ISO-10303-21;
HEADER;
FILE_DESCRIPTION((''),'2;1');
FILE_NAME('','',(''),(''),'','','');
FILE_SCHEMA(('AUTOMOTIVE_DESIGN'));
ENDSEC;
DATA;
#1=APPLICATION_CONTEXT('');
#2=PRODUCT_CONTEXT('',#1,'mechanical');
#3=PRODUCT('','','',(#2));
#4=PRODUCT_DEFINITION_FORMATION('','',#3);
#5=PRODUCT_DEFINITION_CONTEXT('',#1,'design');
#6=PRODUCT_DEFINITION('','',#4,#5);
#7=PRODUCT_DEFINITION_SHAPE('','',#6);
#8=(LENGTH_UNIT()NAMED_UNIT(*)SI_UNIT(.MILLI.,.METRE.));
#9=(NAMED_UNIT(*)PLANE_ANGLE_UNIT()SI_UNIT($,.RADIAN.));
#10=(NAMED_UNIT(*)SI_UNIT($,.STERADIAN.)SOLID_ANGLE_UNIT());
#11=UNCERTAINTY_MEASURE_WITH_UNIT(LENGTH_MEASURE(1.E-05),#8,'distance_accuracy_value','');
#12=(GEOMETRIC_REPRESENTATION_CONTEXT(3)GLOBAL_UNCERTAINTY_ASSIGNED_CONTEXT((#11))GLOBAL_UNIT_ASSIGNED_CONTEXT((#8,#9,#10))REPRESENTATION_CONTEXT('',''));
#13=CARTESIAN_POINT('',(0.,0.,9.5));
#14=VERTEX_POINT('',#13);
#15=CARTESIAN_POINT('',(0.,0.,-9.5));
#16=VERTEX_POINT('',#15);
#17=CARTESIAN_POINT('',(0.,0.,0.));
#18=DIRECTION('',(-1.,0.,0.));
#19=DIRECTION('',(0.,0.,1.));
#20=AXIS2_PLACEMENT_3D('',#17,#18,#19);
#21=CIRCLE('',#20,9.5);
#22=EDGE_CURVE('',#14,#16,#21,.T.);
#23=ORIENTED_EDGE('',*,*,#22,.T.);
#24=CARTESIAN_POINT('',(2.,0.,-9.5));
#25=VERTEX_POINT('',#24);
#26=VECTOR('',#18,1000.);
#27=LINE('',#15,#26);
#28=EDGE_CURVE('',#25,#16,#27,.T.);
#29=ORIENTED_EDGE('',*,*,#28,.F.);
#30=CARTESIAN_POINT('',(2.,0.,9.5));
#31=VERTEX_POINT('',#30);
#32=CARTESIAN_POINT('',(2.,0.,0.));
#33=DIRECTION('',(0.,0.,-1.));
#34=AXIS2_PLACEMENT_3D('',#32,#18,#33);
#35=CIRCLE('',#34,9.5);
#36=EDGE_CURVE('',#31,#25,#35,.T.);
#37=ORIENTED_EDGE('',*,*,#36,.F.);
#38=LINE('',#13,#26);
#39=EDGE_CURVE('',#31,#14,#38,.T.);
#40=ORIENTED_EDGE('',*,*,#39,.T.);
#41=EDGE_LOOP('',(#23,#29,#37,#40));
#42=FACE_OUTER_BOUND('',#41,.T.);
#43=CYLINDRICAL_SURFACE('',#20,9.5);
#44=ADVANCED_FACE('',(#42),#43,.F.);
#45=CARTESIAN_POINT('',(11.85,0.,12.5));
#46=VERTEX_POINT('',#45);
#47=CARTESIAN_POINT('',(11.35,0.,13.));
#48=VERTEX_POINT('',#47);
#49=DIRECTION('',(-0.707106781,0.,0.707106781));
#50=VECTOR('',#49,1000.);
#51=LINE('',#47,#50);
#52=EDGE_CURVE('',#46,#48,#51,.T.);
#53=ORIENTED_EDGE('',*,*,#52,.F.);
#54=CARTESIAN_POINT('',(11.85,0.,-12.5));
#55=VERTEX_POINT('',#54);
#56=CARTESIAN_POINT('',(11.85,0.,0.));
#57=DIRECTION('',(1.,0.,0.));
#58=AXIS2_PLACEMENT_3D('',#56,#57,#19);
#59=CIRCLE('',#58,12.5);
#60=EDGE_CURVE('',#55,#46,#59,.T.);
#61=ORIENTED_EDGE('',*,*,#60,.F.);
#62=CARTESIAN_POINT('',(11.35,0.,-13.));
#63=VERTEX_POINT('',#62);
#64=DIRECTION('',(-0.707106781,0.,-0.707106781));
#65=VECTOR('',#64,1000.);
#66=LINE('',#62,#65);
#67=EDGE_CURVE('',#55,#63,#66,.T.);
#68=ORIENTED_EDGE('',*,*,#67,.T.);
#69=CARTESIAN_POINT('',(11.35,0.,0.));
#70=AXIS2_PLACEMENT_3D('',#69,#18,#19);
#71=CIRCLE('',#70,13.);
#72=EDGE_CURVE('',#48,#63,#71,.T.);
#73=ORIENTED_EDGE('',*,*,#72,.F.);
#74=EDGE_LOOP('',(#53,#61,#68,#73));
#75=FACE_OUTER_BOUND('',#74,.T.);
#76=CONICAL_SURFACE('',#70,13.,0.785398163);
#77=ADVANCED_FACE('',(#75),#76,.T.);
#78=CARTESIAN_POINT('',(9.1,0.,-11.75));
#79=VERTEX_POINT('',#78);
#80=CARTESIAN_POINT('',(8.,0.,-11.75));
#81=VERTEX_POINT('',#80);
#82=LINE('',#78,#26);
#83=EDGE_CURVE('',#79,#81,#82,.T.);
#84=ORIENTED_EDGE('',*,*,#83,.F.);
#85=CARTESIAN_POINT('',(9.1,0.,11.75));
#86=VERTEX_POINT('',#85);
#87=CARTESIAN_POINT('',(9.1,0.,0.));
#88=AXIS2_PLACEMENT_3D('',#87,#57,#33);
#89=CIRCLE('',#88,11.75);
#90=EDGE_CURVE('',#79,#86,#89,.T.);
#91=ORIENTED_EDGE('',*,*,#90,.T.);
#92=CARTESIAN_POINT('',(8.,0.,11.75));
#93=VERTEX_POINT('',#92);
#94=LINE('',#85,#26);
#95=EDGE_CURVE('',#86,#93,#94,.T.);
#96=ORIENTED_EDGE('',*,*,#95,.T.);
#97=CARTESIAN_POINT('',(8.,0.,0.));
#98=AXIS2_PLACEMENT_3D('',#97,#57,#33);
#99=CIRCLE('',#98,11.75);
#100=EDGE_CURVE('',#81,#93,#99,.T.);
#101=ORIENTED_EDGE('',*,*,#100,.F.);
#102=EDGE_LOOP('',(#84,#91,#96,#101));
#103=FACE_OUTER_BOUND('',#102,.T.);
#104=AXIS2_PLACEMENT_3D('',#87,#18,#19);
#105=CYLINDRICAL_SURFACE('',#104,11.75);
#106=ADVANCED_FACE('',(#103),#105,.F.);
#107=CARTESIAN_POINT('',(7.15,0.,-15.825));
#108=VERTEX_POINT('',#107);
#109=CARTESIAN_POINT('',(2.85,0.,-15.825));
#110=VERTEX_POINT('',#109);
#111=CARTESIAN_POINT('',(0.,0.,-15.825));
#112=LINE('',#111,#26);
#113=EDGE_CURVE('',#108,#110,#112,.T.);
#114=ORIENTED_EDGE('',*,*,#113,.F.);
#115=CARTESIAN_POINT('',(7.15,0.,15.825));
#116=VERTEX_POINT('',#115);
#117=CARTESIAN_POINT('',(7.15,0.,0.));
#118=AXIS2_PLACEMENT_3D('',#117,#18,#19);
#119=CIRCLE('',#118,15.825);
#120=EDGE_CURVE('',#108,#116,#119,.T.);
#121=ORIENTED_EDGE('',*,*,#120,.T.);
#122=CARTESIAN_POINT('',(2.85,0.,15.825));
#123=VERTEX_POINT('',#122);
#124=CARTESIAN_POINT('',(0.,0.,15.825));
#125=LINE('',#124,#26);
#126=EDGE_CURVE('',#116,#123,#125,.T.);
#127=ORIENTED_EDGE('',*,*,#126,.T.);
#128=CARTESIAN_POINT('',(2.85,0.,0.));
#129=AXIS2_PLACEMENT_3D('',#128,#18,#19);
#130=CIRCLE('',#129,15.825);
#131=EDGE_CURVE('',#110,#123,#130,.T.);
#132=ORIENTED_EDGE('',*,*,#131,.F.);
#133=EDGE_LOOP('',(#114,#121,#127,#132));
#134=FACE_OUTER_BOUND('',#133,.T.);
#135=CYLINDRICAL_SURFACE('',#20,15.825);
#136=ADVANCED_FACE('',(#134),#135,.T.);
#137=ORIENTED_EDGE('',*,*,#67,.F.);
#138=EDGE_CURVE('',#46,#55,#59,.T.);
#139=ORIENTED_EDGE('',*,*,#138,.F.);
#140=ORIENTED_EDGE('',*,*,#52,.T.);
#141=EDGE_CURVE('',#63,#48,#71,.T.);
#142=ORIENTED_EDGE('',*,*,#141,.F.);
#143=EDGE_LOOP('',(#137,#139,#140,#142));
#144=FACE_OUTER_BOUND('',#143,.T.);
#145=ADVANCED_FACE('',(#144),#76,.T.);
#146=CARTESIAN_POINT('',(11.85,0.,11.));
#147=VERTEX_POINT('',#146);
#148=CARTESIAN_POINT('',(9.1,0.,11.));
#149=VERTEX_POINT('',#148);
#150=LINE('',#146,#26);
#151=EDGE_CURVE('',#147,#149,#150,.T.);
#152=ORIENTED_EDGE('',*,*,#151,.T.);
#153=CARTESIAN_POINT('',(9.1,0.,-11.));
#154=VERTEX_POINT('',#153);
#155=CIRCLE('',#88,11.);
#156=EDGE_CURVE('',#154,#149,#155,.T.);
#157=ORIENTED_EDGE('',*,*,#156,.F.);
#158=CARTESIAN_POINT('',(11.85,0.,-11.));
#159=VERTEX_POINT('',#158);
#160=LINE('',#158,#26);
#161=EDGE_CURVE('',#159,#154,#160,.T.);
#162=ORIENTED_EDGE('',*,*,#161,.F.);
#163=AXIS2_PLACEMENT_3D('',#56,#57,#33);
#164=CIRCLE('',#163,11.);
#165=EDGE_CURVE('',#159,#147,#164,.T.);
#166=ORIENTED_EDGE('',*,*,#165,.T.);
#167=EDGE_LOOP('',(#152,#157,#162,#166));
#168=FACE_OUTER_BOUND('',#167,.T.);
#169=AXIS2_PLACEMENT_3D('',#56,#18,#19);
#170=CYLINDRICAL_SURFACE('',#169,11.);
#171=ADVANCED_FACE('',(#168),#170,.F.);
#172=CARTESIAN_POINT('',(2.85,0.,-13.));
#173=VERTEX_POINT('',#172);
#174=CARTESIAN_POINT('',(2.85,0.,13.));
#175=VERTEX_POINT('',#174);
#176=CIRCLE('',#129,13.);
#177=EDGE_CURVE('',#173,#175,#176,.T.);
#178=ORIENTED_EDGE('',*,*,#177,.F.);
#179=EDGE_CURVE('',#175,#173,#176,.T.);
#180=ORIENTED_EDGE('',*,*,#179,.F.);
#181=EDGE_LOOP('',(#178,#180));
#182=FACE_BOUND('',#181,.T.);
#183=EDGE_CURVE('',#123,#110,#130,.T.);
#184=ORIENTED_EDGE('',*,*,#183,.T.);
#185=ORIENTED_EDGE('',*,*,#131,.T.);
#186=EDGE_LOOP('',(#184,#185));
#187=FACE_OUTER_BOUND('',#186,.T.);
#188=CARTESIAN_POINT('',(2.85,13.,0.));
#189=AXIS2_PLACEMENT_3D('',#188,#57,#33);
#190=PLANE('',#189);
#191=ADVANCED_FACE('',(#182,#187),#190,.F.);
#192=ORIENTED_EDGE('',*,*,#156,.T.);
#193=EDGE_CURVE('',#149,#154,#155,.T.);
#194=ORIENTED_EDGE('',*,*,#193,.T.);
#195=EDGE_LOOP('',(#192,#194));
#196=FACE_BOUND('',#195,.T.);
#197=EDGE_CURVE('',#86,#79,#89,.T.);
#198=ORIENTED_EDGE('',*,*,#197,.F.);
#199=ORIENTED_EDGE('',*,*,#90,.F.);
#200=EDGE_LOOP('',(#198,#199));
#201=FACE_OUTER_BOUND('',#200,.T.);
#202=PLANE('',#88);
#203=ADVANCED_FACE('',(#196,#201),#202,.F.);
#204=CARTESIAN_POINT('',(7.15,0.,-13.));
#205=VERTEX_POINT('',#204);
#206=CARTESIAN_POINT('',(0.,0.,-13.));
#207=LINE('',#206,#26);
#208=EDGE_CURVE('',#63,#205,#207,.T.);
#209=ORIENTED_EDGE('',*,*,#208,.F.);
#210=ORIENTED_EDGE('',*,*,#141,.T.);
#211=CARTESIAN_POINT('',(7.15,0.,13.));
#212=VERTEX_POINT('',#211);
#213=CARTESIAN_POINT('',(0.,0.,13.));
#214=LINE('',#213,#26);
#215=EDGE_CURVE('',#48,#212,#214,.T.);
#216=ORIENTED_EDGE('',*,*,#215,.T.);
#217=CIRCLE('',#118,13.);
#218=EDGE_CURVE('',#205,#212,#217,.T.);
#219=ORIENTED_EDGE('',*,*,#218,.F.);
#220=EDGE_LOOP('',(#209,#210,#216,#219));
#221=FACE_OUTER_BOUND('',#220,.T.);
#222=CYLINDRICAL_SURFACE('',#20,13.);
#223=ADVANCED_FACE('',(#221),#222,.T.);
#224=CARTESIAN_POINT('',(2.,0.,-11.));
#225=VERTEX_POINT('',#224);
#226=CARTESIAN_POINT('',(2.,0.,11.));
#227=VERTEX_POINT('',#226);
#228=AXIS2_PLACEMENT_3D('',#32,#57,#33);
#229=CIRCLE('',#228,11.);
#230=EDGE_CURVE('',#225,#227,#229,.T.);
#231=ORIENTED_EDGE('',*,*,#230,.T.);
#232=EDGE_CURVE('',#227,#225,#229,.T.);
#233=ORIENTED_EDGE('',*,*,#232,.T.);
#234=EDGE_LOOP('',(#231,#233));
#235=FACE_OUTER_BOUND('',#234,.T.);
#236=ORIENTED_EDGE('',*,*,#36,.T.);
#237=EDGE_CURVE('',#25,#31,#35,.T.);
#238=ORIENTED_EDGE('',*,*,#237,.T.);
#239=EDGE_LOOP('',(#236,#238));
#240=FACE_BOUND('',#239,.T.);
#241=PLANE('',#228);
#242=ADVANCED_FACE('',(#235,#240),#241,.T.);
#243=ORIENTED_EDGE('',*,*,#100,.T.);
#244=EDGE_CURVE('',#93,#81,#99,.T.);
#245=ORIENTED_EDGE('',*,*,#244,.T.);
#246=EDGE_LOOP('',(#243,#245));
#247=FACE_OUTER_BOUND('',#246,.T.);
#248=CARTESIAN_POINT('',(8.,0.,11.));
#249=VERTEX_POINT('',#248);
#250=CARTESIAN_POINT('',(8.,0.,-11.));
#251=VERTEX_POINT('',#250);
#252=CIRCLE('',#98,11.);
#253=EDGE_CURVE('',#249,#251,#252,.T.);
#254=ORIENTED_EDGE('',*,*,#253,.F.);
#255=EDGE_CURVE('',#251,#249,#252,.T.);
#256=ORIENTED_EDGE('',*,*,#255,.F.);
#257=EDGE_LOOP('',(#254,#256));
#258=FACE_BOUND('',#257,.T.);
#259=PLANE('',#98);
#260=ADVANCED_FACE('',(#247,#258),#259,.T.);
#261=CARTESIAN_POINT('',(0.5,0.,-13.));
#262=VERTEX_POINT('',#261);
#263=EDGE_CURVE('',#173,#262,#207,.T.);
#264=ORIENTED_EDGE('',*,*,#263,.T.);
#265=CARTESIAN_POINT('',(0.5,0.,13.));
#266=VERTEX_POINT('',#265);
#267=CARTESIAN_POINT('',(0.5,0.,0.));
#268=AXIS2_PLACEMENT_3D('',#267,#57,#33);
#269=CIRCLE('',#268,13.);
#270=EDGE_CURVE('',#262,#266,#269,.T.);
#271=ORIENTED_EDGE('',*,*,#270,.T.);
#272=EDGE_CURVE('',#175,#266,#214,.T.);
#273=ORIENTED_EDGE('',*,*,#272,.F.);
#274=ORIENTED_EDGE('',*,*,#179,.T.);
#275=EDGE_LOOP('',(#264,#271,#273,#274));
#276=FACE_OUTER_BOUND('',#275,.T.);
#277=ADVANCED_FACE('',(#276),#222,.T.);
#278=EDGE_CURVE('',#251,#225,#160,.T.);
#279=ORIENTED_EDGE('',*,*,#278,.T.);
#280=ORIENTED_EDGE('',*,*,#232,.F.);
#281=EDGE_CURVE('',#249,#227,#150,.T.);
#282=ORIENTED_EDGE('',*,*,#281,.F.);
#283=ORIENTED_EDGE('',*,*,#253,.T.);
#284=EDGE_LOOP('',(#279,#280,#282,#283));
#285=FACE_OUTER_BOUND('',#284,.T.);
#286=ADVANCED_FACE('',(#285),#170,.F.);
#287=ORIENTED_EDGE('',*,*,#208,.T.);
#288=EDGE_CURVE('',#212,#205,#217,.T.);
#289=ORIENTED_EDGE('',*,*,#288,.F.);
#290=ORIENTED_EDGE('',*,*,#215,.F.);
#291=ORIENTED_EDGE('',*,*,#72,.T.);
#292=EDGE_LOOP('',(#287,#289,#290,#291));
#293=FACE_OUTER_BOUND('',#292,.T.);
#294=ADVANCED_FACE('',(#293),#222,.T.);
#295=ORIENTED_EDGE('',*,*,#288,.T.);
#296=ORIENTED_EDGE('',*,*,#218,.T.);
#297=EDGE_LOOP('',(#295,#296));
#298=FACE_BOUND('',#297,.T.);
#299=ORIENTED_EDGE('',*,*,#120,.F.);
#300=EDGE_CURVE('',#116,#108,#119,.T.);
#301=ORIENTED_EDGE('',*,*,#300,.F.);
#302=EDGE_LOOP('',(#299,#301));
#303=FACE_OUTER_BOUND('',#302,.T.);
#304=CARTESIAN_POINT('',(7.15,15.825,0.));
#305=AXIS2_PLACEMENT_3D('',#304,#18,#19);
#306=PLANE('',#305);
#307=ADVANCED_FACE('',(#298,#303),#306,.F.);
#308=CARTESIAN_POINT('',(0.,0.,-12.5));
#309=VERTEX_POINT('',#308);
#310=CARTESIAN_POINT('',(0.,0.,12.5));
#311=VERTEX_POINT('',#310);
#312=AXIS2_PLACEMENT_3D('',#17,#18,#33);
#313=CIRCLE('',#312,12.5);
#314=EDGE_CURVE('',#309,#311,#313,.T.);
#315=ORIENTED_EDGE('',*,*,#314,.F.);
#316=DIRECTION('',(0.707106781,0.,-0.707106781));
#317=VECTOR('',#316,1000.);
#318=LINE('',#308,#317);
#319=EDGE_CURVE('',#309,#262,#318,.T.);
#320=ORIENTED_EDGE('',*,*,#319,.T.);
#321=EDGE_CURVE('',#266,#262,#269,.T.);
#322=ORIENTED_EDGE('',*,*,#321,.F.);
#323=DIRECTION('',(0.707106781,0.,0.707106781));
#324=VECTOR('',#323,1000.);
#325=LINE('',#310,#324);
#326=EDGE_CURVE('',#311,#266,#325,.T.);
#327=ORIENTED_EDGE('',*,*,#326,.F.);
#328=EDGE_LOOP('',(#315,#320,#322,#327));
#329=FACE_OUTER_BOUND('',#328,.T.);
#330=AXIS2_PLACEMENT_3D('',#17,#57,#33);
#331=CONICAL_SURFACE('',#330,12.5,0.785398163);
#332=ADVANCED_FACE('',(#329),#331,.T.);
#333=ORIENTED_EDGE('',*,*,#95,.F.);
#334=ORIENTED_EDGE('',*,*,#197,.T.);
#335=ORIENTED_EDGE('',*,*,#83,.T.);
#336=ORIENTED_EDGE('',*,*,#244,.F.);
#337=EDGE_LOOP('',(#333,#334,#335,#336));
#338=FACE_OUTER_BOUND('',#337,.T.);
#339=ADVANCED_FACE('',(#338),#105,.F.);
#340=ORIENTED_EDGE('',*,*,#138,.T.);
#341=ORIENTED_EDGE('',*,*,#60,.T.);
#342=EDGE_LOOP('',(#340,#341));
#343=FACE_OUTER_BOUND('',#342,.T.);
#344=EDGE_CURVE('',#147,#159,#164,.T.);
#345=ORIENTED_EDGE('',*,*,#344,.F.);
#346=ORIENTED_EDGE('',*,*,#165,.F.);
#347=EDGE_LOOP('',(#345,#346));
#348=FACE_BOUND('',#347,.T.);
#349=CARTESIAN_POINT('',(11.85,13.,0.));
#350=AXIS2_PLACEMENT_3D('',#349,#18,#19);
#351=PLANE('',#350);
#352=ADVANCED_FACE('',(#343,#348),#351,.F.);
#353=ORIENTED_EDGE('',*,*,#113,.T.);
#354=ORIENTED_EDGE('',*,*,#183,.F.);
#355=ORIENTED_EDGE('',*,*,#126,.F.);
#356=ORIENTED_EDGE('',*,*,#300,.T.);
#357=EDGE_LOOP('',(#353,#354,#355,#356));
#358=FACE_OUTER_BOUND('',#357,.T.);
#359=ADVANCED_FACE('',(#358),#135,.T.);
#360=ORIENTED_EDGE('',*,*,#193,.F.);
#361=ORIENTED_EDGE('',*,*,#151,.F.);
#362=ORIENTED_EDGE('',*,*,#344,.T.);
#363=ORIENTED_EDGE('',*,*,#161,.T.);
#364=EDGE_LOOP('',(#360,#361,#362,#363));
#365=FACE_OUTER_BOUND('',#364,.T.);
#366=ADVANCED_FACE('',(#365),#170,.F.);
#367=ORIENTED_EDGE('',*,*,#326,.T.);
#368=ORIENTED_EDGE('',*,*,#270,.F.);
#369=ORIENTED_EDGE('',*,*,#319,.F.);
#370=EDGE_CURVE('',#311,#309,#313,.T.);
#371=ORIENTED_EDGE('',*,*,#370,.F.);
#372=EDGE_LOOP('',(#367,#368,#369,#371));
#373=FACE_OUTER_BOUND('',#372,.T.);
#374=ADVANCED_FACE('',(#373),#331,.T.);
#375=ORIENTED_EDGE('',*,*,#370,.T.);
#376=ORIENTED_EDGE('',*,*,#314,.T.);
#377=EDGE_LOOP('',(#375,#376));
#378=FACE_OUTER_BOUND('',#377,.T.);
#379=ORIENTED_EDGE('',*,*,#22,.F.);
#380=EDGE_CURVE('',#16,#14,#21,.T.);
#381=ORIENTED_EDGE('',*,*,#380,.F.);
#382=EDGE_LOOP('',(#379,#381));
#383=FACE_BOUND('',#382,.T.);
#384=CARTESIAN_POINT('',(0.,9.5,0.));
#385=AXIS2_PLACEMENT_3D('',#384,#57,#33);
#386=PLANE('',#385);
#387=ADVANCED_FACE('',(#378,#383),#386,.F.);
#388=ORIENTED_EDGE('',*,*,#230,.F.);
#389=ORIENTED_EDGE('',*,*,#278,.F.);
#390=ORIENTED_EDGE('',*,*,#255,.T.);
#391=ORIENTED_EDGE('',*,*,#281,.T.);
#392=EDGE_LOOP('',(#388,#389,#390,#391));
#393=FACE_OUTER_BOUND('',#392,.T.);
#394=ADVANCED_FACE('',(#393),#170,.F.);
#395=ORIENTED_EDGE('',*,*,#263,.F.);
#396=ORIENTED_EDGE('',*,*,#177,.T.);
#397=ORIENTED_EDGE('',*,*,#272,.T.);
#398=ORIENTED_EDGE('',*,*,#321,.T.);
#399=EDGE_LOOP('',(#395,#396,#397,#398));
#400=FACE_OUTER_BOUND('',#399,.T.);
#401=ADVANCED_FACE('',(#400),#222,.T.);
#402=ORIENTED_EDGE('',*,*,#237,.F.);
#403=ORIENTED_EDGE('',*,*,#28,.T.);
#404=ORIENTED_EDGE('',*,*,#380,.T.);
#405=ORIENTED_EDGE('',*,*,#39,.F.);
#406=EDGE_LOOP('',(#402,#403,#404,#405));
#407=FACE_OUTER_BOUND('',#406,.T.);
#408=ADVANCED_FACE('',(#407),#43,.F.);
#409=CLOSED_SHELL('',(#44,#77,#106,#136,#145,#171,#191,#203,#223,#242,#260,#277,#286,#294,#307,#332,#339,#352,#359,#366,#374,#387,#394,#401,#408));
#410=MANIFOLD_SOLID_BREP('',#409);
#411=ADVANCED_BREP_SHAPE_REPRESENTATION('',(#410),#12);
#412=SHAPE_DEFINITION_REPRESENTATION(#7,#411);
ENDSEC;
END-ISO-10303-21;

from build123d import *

# Parameters (mm, degrees)
CUT_EXTRUDE_START   = 2
SKETCH_2_R          = 11
CUT_EXTRUDE_1_DEPTH = 24.323580908
CUT_EXTRUDE_START_2 = 6
SKETCH_3_R          = 11.75
CUT_EXTRUDE_2_DEPTH = 1.1
CHAMFER_1_SIZE      = 0.5


with BuildPart() as part:
    # 草图1 → 旋转1 (revolve)
    with BuildSketch(Plane.XY, mode=Mode.PRIVATE) as revolve_1_sk:
        Polygon((0, 9.5), (0, 13), (2.85, 13), (2.85, 15.825), (7.15, 15.825), (7.15, 13), (11.85, 13), (11.85, 9.5), align=None)
    revolve(revolve_1_sk.sketch.rotate(Axis((0, 0, 0), (1, 0, 0)), 90), axis=Axis((0, 0, 0), (1, 0, 0)))

    # 草图2 → 切除-拉伸1 (cut, through all)
    with BuildSketch(Plane(origin=(0, 0, 0), x_dir=(0, 0, -1), z_dir=(1, 0, 0)).offset(CUT_EXTRUDE_START)):
        Circle(SKETCH_2_R)
    extrude(amount=CUT_EXTRUDE_1_DEPTH, mode=Mode.SUBTRACT)

    # 草图3 → 切除-拉伸2 (cut)
    with BuildSketch(Plane(origin=(2, 0, 0), x_dir=(0, 0, -1), z_dir=(1, 0, 0)).offset(CUT_EXTRUDE_START_2)):
        Circle(SKETCH_3_R)
    extrude(amount=CUT_EXTRUDE_2_DEPTH, mode=Mode.SUBTRACT)

    # 倒角1
    chamfer_1_edges = [part.edges().sort_by_distance(p)[0] for p in [
        (11.85, 0, -13),
        (0, 0, -13),
    ]]
    chamfer(chamfer_1_edges, length=CHAMFER_1_SIZE)


solid = part.part
